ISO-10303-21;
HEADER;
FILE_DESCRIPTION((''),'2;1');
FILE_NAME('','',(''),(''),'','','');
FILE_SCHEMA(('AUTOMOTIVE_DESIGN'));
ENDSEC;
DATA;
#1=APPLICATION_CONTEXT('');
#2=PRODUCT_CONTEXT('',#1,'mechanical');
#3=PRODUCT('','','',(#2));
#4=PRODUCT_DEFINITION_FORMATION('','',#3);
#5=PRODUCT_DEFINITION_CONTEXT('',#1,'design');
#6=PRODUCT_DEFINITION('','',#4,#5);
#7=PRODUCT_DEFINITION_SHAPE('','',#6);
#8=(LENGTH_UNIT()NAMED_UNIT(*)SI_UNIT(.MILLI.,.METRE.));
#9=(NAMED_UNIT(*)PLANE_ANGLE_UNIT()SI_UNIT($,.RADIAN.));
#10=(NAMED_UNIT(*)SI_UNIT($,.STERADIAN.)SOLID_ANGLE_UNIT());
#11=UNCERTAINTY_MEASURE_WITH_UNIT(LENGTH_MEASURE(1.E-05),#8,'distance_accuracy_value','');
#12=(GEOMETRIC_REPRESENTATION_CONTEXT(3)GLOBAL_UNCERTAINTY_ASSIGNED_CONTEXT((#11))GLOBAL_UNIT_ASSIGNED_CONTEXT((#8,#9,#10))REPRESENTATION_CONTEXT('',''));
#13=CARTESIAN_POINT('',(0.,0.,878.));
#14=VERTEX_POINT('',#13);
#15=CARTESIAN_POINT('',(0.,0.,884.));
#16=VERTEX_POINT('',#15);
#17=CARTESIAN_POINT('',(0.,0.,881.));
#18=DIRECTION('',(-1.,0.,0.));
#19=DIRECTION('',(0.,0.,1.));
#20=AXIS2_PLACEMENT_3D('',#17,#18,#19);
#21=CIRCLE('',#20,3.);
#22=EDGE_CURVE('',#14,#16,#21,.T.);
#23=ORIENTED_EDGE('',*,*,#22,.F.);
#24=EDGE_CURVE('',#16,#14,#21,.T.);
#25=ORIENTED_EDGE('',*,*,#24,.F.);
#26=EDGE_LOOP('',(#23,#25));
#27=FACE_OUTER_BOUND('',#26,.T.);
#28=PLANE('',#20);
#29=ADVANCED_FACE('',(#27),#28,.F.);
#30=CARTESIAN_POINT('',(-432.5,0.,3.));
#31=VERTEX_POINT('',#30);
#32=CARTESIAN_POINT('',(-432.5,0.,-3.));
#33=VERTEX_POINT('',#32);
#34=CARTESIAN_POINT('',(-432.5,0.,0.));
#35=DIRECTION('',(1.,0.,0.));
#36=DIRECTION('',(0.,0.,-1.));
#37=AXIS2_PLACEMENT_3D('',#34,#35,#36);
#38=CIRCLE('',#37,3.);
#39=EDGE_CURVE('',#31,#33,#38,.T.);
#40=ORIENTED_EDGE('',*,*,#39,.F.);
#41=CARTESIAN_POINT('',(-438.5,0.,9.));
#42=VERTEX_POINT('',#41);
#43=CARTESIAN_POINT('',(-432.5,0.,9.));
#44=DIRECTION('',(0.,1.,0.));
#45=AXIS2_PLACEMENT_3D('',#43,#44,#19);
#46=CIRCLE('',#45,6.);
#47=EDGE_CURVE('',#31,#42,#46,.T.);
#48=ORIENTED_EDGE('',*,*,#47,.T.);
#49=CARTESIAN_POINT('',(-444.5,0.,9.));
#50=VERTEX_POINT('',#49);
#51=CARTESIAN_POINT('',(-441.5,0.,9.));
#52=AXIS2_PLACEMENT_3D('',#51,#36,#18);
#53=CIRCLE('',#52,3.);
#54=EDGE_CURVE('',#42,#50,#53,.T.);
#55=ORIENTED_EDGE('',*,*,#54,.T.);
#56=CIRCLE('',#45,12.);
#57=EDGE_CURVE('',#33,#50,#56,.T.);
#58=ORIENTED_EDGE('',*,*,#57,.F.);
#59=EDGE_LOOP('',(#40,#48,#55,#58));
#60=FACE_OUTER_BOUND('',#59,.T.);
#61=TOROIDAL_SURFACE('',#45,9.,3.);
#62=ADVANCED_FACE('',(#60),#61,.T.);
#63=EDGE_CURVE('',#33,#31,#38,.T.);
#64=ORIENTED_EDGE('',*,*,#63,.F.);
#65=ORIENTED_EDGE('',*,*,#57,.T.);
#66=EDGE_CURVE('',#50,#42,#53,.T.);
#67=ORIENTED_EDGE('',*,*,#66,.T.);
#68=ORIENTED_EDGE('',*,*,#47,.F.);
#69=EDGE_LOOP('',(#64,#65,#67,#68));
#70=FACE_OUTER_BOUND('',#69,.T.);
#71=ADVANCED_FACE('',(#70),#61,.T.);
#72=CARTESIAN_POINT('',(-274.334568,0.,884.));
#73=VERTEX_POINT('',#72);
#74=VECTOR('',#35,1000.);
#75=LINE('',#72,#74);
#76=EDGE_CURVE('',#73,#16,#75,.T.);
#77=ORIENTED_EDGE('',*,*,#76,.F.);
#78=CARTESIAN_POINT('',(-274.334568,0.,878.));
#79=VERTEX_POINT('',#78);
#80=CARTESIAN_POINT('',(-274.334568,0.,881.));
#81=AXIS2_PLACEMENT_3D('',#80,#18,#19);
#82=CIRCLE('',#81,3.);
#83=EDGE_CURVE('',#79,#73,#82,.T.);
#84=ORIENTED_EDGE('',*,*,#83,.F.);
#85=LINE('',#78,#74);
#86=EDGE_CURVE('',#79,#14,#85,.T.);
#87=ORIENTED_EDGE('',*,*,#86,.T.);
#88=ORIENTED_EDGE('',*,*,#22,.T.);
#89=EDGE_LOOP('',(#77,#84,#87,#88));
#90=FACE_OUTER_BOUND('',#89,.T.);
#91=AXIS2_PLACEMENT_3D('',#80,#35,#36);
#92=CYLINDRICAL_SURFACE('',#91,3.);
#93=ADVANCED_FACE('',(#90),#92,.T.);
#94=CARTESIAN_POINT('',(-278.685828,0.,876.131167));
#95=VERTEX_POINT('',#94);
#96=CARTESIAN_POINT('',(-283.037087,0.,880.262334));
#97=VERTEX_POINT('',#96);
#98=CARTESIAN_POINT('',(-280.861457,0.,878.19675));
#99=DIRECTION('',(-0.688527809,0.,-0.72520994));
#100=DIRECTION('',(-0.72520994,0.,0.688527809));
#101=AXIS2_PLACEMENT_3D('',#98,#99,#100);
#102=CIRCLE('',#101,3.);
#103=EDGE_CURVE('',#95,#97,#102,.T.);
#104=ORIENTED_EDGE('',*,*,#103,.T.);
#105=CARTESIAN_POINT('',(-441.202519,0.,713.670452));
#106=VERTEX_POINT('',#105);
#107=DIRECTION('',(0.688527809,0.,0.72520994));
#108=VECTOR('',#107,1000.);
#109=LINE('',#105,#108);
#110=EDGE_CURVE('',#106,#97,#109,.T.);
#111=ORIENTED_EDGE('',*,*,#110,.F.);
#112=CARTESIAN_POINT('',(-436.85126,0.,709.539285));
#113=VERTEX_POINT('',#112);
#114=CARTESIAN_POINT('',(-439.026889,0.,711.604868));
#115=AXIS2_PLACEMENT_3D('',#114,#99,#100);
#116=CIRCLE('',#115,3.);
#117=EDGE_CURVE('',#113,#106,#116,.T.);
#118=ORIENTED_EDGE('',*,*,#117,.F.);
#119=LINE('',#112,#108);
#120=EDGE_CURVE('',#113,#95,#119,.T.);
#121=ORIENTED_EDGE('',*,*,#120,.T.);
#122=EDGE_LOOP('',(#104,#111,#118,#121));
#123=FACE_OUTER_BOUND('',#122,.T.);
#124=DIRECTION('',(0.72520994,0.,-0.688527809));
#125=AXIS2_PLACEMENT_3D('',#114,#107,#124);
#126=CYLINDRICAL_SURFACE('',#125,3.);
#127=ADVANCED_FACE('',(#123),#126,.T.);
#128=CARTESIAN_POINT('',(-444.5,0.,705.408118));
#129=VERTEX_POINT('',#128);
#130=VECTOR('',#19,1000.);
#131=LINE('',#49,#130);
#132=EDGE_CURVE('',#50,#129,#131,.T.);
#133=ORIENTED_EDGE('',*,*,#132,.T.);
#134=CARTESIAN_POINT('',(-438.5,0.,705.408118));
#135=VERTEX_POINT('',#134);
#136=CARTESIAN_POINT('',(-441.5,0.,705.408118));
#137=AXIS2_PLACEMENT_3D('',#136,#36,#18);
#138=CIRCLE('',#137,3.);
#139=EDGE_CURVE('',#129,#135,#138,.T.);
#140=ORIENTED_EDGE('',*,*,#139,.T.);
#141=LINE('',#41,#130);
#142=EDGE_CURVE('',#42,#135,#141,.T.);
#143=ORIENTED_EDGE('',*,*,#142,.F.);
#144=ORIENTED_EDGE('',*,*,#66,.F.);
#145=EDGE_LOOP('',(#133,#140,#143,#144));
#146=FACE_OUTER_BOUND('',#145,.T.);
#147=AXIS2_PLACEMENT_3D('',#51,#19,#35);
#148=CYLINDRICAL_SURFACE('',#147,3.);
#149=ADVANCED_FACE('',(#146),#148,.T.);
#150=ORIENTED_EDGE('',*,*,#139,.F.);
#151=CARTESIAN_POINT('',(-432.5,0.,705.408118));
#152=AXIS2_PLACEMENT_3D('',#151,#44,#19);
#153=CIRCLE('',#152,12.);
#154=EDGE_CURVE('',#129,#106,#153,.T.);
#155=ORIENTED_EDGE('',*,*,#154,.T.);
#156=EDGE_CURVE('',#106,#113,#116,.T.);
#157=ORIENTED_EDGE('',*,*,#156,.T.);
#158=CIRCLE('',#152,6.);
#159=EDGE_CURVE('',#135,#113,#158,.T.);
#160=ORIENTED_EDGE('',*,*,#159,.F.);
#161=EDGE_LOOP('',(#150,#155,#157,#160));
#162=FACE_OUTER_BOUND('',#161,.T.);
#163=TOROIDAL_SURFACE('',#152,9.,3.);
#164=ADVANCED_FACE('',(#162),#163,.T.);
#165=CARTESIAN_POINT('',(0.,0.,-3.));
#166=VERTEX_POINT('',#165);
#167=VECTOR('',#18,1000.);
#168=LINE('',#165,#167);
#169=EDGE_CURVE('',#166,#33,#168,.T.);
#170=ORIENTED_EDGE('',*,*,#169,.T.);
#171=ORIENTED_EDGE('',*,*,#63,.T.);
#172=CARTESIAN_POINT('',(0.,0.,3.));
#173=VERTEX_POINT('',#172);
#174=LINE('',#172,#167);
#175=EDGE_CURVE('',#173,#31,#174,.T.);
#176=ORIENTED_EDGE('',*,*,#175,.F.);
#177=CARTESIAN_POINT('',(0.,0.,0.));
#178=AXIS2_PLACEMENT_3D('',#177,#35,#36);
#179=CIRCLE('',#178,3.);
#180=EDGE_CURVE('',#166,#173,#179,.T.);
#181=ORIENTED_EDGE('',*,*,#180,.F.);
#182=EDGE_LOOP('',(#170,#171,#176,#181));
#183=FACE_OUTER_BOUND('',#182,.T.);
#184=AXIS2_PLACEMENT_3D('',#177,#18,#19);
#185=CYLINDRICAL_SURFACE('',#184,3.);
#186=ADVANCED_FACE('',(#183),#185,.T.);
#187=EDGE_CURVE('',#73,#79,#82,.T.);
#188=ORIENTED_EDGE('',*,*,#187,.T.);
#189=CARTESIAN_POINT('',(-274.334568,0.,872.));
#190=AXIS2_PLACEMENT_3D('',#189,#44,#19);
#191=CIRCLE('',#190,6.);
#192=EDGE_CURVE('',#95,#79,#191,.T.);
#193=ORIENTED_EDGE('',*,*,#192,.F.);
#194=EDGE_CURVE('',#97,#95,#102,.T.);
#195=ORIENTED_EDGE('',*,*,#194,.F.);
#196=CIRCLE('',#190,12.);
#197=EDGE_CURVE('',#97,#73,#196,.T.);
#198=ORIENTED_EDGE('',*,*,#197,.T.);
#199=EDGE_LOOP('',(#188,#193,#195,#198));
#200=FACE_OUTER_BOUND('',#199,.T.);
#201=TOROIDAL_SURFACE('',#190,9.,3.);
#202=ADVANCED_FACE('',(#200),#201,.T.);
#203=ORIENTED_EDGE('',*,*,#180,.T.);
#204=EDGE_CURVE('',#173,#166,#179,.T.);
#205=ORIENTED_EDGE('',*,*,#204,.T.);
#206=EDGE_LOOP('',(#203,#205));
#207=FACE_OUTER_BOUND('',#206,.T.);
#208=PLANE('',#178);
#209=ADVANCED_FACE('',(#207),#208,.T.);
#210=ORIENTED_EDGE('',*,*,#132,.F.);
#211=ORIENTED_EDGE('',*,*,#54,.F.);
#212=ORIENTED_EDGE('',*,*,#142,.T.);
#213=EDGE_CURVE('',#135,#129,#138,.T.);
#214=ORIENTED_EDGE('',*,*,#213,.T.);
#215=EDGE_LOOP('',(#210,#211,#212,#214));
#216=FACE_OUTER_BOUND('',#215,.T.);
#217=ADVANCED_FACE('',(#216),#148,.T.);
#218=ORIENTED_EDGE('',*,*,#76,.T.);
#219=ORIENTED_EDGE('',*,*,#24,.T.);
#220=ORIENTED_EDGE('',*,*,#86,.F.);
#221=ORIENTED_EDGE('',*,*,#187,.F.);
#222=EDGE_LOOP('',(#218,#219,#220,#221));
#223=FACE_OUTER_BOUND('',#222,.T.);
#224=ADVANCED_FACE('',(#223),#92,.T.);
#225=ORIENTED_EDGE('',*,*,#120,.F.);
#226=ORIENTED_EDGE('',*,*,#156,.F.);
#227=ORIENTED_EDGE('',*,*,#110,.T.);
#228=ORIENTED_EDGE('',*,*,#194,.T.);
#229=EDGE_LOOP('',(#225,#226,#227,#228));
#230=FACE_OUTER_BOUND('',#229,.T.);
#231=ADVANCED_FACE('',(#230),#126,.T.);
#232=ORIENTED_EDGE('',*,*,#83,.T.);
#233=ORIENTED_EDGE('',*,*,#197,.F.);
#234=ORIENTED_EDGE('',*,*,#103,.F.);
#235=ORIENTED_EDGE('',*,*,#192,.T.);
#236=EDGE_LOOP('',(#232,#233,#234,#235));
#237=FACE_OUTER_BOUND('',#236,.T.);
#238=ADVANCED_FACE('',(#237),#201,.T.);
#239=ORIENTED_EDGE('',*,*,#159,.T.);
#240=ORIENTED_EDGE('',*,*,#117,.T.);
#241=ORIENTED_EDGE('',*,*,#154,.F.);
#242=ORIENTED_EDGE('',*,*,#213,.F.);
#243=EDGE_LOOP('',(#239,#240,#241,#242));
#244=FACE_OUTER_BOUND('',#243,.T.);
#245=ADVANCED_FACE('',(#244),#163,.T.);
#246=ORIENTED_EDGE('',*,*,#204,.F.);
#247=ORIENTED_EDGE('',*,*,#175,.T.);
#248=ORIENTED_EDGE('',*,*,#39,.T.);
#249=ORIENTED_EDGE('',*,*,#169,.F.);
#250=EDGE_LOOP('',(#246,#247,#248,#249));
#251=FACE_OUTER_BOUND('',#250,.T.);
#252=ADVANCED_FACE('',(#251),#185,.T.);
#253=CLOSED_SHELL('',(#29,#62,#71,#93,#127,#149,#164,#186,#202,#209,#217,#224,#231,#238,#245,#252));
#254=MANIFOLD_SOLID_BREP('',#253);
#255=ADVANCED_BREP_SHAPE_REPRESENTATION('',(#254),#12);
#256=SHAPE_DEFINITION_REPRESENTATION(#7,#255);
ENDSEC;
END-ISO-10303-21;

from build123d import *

# Parameters (mm, degrees)
SKETCH2_R = 3


with BuildPart() as part:
    # Sweep1: sweep along a path in Sketch1
    with BuildLine(Plane(origin=(0, 0, 0), x_dir=(1, 0, 0), z_dir=(0, 1, 0))) as sweep1_path:
        Line((0, 0), (-432.5, 0))
        ThreePointArc((-432.5, 0), (-438.863961031, -2.636038969), (-441.5, -9))
        Line((-441.5, -9), (-441.5, -705.408118144))
        ThreePointArc((-441.5, -705.408118144), (-440.858887638, -708.744133349), (-439.026889456, -711.604868424))
        Line((-439.026889456, -711.604868424), (-280.861457438, -878.19675028))
        ThreePointArc((-280.861457438, -878.19675028), (-277.886275141, -880.269545106), (-274.334567982, -881))
        Line((-274.334567982, -881), (0, -881))
    # Sketch2 → Sweep1 (sweep)
    with BuildSketch(Plane(origin=(0, 0, 0), x_dir=(0, 0, -1), z_dir=(1, 0, 0))):
        Circle(SKETCH2_R)
    sweep(path=sweep1_path.line)


solid = part.part
